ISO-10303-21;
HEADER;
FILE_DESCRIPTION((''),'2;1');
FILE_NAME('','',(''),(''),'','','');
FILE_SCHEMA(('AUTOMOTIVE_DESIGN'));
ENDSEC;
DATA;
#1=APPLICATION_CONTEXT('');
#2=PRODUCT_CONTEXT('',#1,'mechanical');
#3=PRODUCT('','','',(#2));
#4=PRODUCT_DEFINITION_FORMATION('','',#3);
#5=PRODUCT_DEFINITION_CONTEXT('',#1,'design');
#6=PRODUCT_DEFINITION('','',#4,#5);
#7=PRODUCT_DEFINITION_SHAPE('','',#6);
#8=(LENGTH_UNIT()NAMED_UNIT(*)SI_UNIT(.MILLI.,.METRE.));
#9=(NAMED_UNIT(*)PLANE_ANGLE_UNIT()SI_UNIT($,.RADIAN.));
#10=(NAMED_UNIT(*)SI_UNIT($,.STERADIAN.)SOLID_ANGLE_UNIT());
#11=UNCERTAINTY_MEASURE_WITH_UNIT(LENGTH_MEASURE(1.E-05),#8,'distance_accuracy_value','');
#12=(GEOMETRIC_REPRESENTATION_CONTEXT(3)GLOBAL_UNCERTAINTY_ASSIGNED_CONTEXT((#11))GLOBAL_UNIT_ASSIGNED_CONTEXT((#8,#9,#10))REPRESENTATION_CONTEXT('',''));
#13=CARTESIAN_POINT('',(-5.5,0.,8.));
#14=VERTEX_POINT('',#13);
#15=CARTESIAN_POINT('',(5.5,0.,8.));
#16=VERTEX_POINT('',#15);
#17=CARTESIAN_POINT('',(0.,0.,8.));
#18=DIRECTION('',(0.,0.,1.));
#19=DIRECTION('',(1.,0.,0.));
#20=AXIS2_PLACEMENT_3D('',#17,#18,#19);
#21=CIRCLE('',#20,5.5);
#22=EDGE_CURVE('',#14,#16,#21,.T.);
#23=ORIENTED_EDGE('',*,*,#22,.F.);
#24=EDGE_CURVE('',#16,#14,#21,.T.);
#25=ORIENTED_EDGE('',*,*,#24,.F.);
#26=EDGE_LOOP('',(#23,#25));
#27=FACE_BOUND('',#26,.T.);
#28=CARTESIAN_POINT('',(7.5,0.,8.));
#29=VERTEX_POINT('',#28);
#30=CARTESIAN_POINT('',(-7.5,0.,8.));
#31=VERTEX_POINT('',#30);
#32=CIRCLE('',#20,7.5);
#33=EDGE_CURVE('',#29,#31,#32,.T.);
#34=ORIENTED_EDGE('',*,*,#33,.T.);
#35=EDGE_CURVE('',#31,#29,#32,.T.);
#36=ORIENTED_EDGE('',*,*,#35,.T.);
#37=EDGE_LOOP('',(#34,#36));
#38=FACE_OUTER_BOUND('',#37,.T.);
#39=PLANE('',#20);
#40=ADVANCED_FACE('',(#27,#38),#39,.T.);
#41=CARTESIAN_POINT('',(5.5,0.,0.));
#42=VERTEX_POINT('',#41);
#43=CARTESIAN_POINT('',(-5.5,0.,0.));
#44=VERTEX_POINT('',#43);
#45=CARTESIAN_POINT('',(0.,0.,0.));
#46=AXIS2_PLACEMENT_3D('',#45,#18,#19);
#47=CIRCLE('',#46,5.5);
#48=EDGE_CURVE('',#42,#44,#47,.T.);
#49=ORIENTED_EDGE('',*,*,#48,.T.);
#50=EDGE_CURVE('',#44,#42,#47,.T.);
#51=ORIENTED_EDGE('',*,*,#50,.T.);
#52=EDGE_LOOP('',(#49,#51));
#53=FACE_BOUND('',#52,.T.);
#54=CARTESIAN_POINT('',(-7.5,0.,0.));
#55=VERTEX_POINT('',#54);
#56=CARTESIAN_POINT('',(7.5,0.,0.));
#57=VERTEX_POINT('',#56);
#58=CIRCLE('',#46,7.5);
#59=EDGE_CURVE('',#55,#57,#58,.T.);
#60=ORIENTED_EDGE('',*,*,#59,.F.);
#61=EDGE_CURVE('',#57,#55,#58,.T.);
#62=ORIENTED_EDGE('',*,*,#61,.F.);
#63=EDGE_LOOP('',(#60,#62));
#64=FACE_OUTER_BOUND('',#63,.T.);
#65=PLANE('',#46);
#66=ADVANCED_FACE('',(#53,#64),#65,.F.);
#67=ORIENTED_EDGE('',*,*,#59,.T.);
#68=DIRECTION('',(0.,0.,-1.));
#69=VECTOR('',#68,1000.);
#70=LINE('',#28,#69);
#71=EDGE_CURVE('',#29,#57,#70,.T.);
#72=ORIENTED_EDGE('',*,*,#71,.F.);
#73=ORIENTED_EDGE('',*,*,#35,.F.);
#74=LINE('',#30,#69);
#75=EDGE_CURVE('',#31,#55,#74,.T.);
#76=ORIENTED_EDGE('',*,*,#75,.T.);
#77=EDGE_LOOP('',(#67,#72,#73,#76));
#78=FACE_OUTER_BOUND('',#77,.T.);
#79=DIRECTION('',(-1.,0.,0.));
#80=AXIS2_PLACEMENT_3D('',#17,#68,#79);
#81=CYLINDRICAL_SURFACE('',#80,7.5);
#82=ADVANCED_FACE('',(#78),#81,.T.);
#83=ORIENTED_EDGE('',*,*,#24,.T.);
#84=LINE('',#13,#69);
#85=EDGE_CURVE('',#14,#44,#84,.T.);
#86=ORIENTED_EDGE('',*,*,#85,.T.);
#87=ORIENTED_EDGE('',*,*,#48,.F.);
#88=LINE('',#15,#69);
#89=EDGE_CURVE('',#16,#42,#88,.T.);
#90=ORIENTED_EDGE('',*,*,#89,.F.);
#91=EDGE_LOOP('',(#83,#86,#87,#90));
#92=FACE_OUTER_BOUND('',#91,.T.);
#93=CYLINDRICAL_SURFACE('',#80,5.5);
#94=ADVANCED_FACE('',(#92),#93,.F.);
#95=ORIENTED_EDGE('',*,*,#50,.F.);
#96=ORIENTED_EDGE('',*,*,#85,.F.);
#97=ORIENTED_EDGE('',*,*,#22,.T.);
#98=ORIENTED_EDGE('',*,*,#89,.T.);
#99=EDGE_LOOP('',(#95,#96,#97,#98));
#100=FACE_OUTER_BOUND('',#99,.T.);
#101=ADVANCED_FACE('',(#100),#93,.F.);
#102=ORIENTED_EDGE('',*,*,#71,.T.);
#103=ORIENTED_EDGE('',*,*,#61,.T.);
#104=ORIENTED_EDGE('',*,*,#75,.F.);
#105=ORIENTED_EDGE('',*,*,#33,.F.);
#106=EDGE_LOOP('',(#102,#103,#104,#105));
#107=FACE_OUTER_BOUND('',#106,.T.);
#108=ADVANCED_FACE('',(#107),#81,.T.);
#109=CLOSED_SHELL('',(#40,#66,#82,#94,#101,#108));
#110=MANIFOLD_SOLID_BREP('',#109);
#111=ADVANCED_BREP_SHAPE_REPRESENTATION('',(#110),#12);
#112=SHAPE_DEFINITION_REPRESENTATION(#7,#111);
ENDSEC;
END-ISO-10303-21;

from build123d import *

# Parameters (mm, degrees)
SKETCH_1_R      = 7.5
SKETCH_1_R_2    = 5.5
EXTRUDE_1_DEPTH = 8


with BuildPart() as part:
    # 草图1 → 凸台-拉伸1 (new body)
    with BuildSketch(Plane.XY):
        Circle(SKETCH_1_R)
        Circle(SKETCH_1_R_2, mode=Mode.SUBTRACT)
    extrude(amount=EXTRUDE_1_DEPTH)


solid = part.part
